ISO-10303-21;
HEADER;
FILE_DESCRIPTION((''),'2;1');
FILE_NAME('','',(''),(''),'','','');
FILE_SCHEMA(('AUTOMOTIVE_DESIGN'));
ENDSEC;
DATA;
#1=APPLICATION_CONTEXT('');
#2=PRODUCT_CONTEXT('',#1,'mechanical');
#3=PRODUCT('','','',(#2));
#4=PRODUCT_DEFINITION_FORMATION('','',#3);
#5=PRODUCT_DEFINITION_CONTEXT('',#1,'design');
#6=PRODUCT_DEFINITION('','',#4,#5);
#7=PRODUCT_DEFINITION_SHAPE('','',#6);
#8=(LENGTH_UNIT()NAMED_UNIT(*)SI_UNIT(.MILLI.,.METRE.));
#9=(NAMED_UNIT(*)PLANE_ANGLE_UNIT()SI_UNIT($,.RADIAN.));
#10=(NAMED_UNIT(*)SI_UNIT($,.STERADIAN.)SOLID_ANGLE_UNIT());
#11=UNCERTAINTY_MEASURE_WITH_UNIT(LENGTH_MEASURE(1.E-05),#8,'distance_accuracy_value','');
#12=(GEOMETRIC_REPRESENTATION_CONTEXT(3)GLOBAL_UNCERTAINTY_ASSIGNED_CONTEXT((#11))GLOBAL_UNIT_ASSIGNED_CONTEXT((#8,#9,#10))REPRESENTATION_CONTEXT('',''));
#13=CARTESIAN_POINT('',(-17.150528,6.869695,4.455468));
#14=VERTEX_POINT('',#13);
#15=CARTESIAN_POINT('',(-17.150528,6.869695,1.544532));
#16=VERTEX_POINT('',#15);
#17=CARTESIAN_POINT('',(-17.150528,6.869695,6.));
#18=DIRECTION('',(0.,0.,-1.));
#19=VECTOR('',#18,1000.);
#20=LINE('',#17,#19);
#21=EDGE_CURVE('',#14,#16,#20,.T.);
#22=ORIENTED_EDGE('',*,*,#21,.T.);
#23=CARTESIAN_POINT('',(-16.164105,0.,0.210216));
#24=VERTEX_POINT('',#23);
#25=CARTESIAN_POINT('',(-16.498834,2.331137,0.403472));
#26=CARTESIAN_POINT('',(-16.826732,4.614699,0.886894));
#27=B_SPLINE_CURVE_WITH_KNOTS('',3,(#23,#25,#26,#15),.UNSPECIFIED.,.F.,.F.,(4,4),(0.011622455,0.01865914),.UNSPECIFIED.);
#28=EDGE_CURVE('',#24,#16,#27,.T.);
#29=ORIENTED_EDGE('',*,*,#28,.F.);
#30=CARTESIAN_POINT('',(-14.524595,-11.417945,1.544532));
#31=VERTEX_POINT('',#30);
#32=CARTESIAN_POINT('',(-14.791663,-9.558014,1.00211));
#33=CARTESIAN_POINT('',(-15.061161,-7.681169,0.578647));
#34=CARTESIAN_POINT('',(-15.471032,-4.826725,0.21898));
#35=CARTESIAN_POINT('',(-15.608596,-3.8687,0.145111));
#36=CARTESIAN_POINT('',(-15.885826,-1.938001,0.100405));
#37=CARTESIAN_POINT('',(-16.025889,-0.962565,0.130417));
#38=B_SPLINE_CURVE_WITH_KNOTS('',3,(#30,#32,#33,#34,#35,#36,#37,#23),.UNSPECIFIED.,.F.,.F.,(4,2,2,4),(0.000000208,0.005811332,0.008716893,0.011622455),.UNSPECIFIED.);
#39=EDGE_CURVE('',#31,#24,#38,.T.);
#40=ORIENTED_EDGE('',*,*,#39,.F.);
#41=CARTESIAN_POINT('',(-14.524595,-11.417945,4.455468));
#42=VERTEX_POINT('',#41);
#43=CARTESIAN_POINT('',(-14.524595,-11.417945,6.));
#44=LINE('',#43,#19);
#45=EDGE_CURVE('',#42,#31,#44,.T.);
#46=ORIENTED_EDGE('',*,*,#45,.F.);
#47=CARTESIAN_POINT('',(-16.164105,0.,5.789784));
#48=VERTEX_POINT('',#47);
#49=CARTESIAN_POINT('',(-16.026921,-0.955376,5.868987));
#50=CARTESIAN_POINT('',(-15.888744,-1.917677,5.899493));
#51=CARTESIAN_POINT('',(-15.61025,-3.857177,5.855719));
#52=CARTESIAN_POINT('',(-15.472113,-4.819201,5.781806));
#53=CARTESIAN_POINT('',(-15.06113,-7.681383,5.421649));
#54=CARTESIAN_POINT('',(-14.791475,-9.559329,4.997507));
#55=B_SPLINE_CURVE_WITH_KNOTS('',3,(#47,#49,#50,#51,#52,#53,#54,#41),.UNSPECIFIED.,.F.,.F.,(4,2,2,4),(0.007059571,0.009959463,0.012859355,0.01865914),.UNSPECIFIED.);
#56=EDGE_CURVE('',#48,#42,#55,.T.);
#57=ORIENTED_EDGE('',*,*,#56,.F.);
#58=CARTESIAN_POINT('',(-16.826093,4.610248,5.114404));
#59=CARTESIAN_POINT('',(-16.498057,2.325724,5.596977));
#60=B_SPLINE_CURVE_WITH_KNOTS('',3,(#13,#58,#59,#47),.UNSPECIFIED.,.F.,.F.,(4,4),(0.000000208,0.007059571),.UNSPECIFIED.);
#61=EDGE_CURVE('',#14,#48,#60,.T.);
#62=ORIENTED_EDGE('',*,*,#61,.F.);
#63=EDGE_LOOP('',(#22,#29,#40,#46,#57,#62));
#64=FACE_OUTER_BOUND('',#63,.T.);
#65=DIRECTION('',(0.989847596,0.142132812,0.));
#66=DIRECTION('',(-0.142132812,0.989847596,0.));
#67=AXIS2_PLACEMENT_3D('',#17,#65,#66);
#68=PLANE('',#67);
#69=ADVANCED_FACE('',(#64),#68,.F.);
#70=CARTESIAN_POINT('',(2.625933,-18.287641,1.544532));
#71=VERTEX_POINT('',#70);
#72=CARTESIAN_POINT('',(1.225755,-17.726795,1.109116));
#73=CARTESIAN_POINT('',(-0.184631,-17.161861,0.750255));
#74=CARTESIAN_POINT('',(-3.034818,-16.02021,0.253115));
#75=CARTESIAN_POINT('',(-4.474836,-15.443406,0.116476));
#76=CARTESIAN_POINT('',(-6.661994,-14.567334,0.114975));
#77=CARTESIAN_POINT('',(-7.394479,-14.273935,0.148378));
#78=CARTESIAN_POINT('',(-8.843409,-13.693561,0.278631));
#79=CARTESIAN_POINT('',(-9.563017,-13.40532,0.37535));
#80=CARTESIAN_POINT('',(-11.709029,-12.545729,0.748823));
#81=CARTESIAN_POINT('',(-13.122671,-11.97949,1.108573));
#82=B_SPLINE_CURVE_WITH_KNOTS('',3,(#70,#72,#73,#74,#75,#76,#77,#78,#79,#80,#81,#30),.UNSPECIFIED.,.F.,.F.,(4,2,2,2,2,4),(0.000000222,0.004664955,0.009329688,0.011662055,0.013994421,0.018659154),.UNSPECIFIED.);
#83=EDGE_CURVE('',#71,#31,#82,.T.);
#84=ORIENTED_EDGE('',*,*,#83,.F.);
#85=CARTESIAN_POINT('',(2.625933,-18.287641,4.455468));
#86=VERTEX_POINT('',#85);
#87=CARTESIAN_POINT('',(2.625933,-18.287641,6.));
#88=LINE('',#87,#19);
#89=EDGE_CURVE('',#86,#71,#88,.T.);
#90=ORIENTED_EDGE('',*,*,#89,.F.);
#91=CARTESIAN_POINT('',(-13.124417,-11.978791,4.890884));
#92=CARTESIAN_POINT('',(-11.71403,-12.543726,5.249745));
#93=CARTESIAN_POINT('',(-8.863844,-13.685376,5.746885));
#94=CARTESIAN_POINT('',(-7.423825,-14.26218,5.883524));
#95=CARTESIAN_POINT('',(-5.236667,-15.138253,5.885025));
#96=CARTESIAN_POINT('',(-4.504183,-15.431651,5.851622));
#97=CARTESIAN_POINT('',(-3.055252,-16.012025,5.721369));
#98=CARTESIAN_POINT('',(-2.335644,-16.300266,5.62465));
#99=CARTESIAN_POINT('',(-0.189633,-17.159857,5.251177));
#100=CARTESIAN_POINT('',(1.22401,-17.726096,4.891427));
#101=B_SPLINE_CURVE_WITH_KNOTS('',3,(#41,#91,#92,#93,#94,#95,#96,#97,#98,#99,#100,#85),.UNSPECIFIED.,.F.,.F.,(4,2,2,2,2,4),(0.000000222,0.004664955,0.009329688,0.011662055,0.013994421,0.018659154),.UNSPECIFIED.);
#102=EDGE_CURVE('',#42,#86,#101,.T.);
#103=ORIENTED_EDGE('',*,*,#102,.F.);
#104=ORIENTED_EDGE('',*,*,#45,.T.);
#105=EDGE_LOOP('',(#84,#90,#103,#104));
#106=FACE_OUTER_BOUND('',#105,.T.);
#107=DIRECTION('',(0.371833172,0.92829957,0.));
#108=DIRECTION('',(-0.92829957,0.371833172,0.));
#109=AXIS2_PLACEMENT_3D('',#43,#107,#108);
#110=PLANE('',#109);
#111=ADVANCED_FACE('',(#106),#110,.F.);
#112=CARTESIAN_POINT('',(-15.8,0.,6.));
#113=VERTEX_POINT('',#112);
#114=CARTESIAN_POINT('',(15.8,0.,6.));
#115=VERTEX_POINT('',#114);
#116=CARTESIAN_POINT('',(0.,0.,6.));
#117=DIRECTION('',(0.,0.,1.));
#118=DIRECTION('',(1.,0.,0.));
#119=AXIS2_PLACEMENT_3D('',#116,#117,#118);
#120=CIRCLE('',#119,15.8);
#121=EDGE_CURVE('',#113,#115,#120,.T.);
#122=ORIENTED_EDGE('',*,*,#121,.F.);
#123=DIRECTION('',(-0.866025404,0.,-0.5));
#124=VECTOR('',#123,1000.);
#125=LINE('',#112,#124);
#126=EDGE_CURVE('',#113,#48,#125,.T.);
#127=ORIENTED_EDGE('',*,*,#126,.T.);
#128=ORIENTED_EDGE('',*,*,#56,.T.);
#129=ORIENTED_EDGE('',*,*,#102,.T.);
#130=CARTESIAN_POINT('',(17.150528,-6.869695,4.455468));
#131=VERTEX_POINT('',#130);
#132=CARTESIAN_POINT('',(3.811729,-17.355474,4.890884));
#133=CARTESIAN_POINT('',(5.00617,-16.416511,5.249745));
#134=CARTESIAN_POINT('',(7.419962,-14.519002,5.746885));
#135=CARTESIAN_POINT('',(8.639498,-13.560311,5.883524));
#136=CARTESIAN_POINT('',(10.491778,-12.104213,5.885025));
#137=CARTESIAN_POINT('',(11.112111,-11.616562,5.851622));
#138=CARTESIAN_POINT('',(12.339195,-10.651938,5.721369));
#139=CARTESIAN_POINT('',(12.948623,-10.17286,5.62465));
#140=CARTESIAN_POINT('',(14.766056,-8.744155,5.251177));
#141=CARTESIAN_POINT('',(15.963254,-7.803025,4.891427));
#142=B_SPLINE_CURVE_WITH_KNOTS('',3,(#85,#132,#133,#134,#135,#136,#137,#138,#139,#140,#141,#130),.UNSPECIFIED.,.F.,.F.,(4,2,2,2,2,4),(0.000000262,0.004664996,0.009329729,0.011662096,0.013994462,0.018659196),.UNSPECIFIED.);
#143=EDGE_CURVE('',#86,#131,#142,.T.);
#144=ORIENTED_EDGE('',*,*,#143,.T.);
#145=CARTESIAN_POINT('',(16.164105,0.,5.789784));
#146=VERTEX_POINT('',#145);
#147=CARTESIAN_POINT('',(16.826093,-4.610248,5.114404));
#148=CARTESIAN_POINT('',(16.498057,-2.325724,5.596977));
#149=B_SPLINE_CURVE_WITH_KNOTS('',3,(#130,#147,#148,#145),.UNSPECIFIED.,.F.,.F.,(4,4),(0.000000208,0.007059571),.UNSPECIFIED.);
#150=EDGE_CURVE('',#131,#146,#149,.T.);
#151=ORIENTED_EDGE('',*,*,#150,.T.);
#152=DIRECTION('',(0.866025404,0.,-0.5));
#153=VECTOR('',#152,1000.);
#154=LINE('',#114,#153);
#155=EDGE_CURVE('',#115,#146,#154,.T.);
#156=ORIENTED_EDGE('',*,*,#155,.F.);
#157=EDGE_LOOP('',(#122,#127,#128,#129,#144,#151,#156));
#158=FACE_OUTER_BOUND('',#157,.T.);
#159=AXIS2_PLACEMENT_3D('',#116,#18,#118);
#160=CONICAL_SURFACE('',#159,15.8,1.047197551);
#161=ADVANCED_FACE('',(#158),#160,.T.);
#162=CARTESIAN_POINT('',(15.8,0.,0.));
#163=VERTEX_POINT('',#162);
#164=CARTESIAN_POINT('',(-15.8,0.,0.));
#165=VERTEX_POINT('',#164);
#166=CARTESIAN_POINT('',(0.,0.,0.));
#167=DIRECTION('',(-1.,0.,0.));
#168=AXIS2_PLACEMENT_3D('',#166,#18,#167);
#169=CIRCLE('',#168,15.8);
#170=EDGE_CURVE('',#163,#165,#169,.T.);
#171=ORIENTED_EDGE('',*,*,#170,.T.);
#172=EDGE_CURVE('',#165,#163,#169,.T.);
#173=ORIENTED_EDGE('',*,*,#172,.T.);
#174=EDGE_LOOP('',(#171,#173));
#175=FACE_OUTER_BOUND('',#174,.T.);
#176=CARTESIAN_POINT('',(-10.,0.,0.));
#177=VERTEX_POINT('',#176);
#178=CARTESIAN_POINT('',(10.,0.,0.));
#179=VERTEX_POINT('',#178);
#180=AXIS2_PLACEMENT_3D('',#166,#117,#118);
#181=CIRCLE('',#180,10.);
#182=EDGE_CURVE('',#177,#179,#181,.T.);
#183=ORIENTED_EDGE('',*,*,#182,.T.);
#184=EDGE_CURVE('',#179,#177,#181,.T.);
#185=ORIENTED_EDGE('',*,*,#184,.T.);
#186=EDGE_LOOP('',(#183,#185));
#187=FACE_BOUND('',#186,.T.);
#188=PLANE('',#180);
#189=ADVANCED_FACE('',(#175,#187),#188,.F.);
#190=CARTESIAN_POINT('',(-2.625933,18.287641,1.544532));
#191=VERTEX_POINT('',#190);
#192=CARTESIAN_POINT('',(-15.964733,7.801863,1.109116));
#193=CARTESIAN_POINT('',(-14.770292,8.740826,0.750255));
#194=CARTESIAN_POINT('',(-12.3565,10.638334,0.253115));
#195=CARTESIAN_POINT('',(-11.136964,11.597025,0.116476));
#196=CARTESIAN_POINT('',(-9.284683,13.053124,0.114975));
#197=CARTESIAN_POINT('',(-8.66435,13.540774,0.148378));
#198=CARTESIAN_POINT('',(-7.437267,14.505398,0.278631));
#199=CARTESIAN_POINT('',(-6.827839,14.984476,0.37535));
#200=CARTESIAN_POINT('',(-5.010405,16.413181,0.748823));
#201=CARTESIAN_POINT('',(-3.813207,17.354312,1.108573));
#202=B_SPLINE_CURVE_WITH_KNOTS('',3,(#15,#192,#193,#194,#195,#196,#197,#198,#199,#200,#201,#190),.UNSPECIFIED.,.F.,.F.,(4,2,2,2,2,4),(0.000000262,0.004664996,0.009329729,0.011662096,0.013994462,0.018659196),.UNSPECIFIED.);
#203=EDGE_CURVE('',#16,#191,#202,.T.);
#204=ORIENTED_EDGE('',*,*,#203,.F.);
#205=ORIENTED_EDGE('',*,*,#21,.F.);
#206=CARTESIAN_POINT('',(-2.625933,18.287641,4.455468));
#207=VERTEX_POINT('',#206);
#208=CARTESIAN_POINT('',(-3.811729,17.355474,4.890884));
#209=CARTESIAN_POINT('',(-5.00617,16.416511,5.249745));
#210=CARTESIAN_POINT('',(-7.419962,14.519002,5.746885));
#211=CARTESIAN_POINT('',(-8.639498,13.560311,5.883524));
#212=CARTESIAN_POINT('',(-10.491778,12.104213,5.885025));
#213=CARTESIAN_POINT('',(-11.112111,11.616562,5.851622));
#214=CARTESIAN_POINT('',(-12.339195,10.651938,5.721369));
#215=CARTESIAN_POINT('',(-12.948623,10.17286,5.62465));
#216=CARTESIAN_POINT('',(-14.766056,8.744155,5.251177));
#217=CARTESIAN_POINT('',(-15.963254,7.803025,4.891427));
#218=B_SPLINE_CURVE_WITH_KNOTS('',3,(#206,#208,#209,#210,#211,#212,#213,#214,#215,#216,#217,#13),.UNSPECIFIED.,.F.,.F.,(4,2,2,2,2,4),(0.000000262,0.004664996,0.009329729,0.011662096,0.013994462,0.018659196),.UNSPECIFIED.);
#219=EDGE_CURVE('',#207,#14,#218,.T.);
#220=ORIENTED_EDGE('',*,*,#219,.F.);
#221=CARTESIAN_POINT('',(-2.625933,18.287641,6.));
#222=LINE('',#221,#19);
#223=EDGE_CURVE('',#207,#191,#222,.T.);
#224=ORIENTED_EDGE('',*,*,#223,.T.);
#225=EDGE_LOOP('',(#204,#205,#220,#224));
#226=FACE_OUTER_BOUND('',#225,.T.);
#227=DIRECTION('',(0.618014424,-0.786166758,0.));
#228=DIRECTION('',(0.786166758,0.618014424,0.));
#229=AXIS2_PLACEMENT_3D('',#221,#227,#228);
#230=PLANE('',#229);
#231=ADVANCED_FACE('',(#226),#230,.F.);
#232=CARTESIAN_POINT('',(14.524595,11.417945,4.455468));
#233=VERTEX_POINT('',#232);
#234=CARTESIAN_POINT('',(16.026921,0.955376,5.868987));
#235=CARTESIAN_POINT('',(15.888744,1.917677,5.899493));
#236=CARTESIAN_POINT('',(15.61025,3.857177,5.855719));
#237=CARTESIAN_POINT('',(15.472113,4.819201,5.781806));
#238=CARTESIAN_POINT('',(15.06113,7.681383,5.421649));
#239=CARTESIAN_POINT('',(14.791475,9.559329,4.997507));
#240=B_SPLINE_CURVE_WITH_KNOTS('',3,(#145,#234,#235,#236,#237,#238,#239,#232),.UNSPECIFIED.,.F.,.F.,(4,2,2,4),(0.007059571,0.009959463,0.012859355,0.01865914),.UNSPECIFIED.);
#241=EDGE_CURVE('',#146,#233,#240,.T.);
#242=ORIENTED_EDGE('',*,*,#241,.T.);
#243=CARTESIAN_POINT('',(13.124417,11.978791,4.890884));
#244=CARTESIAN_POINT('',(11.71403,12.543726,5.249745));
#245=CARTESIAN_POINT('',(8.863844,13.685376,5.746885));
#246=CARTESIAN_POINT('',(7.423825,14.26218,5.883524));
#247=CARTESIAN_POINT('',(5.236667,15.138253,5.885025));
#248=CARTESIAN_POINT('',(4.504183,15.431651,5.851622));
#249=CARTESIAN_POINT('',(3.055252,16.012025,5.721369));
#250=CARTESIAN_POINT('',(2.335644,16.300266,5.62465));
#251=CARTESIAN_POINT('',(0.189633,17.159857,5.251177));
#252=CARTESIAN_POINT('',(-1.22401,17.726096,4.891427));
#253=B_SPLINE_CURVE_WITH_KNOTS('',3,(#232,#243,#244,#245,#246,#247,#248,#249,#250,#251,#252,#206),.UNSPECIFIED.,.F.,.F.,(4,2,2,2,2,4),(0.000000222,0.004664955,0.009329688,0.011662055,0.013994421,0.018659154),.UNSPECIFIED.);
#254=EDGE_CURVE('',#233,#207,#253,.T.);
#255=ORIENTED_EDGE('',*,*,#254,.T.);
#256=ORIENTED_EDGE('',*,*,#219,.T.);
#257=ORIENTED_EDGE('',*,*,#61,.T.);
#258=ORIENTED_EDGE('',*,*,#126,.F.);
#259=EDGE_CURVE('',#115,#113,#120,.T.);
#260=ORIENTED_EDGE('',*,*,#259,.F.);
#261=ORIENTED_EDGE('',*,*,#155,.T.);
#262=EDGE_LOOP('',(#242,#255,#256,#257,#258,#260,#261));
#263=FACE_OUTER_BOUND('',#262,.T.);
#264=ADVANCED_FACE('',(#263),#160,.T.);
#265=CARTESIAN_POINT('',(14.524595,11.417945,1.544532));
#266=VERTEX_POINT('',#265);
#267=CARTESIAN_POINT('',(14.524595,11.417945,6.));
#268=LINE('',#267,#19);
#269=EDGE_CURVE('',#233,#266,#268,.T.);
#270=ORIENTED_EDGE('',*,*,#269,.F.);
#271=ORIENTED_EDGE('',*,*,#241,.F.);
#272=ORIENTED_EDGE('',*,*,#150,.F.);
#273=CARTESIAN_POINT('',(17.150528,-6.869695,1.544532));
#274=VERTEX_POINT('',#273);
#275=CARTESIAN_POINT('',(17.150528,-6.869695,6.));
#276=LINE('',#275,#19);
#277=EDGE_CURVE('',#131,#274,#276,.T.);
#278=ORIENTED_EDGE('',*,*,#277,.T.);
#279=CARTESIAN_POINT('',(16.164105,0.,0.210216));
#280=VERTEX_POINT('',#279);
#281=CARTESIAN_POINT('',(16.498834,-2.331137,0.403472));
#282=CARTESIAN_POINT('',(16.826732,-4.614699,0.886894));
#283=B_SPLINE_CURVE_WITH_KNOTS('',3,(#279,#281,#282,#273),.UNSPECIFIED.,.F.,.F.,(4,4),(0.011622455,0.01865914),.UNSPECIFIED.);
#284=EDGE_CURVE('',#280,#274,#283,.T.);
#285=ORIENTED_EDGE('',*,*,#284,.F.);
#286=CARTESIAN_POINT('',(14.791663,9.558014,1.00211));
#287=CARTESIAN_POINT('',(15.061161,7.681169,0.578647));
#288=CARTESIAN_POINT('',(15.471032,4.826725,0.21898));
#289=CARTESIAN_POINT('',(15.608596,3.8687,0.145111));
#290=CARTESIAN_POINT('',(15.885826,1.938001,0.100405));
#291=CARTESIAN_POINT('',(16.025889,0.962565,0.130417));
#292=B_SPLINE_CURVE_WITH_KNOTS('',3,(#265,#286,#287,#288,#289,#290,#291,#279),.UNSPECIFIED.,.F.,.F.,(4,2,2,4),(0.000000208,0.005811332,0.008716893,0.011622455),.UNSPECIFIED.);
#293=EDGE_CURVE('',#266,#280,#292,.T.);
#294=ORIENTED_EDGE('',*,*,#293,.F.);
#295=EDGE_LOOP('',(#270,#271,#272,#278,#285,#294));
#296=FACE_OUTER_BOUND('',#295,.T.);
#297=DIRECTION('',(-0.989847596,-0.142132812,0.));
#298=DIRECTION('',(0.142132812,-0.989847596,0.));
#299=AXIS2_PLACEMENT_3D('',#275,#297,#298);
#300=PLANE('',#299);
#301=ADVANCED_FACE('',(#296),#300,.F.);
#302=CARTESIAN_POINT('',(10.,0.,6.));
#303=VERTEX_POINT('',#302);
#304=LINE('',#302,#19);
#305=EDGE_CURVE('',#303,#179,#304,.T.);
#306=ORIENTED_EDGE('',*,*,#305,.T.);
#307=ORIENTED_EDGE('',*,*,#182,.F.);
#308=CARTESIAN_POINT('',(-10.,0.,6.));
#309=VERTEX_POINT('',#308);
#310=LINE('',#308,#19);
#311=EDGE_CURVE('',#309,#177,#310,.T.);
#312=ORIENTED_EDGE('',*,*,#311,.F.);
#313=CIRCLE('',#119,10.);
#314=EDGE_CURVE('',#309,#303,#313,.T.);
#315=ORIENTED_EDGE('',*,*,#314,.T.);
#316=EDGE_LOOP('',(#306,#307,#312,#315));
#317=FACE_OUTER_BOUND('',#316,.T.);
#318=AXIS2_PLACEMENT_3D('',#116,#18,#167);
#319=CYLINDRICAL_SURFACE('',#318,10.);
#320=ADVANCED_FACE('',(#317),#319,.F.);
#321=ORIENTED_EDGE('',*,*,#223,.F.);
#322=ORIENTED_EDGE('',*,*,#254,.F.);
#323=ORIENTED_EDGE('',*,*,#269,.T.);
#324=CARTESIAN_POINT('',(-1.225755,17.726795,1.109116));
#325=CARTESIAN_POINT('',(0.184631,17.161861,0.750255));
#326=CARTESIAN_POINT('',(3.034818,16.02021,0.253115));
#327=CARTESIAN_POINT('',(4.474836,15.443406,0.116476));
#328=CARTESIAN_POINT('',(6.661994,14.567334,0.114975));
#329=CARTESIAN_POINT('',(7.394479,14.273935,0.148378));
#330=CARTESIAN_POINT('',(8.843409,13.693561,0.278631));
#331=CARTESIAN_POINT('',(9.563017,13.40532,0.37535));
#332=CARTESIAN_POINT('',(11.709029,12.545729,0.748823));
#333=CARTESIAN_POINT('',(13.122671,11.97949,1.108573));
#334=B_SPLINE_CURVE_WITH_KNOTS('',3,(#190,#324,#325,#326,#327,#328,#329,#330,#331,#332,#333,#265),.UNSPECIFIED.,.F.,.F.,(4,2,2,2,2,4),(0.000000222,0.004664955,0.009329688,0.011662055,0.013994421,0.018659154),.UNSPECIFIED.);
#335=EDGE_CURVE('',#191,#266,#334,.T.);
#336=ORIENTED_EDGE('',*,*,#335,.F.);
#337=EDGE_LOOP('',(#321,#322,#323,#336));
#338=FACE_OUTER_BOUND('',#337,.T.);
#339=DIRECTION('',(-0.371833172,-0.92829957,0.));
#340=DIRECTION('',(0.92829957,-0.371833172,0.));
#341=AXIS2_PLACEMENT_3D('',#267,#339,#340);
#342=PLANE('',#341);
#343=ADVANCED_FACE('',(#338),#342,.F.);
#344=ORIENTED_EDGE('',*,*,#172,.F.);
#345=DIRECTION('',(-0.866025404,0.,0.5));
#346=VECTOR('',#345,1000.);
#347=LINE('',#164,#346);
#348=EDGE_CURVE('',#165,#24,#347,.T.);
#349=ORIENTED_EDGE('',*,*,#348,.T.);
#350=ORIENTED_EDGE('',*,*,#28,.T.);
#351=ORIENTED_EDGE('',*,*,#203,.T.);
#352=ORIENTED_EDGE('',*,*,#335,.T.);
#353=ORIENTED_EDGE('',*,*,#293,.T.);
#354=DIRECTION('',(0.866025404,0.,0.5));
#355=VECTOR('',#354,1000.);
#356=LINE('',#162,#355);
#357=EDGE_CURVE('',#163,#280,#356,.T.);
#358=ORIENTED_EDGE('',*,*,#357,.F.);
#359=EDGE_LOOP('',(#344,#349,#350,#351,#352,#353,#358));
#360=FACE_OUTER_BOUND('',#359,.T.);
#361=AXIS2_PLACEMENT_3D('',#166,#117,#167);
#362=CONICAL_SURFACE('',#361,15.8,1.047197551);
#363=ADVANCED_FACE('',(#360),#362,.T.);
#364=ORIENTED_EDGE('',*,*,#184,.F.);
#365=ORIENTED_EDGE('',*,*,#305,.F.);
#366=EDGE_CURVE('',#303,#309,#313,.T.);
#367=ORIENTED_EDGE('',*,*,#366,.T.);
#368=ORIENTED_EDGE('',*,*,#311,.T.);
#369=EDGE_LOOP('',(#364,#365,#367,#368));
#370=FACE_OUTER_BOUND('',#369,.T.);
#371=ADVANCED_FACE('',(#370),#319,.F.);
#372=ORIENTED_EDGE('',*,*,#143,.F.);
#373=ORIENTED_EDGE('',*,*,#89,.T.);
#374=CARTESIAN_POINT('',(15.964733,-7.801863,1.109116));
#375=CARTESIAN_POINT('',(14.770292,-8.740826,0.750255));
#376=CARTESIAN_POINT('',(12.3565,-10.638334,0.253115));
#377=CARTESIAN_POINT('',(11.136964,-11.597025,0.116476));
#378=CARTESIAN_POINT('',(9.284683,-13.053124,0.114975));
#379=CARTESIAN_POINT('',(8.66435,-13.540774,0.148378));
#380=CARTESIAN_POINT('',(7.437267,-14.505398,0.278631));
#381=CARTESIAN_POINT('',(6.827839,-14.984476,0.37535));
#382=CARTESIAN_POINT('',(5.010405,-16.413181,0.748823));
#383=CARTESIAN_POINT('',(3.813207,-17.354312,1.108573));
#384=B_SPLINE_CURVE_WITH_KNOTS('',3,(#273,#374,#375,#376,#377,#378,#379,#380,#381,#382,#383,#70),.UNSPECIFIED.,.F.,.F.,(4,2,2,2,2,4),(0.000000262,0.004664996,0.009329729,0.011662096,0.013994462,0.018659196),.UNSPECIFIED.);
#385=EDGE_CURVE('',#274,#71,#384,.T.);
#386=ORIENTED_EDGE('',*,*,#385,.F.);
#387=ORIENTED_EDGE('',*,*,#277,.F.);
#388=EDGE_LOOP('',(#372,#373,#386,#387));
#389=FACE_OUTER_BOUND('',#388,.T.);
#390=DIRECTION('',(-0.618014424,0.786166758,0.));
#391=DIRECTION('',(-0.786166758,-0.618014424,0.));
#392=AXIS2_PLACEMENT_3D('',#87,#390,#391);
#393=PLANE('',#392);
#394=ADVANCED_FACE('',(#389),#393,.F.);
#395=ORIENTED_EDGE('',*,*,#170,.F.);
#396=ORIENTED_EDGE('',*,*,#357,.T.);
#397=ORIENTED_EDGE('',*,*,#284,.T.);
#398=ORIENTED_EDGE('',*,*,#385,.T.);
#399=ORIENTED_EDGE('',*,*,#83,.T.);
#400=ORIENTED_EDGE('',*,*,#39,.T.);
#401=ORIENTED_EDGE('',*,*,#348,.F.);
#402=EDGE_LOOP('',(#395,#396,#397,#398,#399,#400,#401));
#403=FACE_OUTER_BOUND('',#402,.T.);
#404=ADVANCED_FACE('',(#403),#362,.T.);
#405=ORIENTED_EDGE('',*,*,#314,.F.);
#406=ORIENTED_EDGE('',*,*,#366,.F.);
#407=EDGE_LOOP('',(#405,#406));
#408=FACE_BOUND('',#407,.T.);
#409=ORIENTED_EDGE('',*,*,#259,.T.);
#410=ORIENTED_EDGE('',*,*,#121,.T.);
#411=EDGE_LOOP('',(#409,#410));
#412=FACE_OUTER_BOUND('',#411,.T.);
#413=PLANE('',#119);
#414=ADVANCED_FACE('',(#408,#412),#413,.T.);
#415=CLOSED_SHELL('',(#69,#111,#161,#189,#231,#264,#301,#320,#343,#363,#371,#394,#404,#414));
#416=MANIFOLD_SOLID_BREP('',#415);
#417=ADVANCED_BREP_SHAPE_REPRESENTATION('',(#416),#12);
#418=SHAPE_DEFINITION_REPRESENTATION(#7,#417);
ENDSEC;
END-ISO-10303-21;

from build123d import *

# Parameters (mm, degrees)
SKETCH1_R           = 10
BOSS_EXTRUDE1_DEPTH = 6
SKETCH3_OUTSIDE_W   = 81.044
SKETCH3_OUTSIDE_H   = 83.318
SKETCH3_OUTSIDE_R   = 15.8
CUT_EXTRUDE2_DEPTH  = 10
CUT_EXTRUDE2_DRAFT  = -60
SKETCH4_OUTSIDE_W   = 63.722
SKETCH4_OUTSIDE_H   = 65.996
SKETCH4_OUTSIDE_R   = 15.8
CUT_EXTRUDE3_DEPTH  = 5
CUT_EXTRUDE3_DRAFT  = -60


with BuildPart() as part:
    # Sketch1 → Boss-Extrude1 (new body)
    with BuildSketch(Plane.XY):
        Polygon((-14.524594865, -11.417945408), (2.62593335, -18.287640837), (17.150528215, -6.869695429), (14.524594865, 11.417945408), (-2.62593335, 18.287640837), (-17.150528215, 6.869695429), align=None)
        Circle(SKETCH1_R, mode=Mode.SUBTRACT)
    extrude(amount=BOSS_EXTRUDE1_DEPTH)


with BuildPart() as cut_extrude2_tool:
    # Sketch3 outside → Cut-Extrude2 (with draft: the straight prism first)
    with BuildSketch(Plane.XY.offset(6)):
        Rectangle(SKETCH3_OUTSIDE_W, SKETCH3_OUTSIDE_H)
        Circle(SKETCH3_OUTSIDE_R, mode=Mode.SUBTRACT)
    extrude(amount=-CUT_EXTRUDE2_DEPTH)
    # Cut-Extrude2: the draft: its side faces are tilted about the plane it starts from
    cut_extrude2_sides = [cut_extrude2_tool.faces().sort_by_distance(p)[0] for p in [
        (0, -41.659, 1),
        (40.522, 0, 1),
        (0, 41.659, 1),
        (-40.522, 0, 1),
        (-15.8, 0, 1),
    ]]
    draft(cut_extrude2_sides, Plane.XY.offset(6), CUT_EXTRUDE2_DRAFT)


with BuildPart() as part_1:
    add(part.part)

    # Cut-Extrude2: cut by cut_extrude2_tool
    add(cut_extrude2_tool.part, mode=Mode.SUBTRACT)


with BuildPart() as cut_extrude3_tool:
    # Sketch4 outside → Cut-Extrude3 (with draft: the straight prism first)
    with BuildSketch(Plane(origin=(0, 0, 0), x_dir=(-1, 0, 0), z_dir=(0, 0, -1))):
        Rectangle(SKETCH4_OUTSIDE_W, SKETCH4_OUTSIDE_H)
        Circle(SKETCH4_OUTSIDE_R, mode=Mode.SUBTRACT)
    extrude(amount=-CUT_EXTRUDE3_DEPTH)
    # Cut-Extrude3: the draft: its side faces are tilted about the plane it starts from
    cut_extrude3_sides = [cut_extrude3_tool.faces().sort_by_distance(p)[0] for p in [
        (0, -32.998, 2.5),
        (-31.861, 0, 2.5),
        (0, 32.998, 2.5),
        (31.861, 0, 2.5),
        (15.8, 0, 2.5),
    ]]
    draft(cut_extrude3_sides, Plane(origin=(0, 0, 0), x_dir=(-1, 0, 0), z_dir=(0, 0, -1)), CUT_EXTRUDE3_DRAFT)


with BuildPart() as part_2:
    add(part_1.part)

    # Cut-Extrude3: cut by cut_extrude3_tool
    add(cut_extrude3_tool.part, mode=Mode.SUBTRACT)


solid = part_2.part
